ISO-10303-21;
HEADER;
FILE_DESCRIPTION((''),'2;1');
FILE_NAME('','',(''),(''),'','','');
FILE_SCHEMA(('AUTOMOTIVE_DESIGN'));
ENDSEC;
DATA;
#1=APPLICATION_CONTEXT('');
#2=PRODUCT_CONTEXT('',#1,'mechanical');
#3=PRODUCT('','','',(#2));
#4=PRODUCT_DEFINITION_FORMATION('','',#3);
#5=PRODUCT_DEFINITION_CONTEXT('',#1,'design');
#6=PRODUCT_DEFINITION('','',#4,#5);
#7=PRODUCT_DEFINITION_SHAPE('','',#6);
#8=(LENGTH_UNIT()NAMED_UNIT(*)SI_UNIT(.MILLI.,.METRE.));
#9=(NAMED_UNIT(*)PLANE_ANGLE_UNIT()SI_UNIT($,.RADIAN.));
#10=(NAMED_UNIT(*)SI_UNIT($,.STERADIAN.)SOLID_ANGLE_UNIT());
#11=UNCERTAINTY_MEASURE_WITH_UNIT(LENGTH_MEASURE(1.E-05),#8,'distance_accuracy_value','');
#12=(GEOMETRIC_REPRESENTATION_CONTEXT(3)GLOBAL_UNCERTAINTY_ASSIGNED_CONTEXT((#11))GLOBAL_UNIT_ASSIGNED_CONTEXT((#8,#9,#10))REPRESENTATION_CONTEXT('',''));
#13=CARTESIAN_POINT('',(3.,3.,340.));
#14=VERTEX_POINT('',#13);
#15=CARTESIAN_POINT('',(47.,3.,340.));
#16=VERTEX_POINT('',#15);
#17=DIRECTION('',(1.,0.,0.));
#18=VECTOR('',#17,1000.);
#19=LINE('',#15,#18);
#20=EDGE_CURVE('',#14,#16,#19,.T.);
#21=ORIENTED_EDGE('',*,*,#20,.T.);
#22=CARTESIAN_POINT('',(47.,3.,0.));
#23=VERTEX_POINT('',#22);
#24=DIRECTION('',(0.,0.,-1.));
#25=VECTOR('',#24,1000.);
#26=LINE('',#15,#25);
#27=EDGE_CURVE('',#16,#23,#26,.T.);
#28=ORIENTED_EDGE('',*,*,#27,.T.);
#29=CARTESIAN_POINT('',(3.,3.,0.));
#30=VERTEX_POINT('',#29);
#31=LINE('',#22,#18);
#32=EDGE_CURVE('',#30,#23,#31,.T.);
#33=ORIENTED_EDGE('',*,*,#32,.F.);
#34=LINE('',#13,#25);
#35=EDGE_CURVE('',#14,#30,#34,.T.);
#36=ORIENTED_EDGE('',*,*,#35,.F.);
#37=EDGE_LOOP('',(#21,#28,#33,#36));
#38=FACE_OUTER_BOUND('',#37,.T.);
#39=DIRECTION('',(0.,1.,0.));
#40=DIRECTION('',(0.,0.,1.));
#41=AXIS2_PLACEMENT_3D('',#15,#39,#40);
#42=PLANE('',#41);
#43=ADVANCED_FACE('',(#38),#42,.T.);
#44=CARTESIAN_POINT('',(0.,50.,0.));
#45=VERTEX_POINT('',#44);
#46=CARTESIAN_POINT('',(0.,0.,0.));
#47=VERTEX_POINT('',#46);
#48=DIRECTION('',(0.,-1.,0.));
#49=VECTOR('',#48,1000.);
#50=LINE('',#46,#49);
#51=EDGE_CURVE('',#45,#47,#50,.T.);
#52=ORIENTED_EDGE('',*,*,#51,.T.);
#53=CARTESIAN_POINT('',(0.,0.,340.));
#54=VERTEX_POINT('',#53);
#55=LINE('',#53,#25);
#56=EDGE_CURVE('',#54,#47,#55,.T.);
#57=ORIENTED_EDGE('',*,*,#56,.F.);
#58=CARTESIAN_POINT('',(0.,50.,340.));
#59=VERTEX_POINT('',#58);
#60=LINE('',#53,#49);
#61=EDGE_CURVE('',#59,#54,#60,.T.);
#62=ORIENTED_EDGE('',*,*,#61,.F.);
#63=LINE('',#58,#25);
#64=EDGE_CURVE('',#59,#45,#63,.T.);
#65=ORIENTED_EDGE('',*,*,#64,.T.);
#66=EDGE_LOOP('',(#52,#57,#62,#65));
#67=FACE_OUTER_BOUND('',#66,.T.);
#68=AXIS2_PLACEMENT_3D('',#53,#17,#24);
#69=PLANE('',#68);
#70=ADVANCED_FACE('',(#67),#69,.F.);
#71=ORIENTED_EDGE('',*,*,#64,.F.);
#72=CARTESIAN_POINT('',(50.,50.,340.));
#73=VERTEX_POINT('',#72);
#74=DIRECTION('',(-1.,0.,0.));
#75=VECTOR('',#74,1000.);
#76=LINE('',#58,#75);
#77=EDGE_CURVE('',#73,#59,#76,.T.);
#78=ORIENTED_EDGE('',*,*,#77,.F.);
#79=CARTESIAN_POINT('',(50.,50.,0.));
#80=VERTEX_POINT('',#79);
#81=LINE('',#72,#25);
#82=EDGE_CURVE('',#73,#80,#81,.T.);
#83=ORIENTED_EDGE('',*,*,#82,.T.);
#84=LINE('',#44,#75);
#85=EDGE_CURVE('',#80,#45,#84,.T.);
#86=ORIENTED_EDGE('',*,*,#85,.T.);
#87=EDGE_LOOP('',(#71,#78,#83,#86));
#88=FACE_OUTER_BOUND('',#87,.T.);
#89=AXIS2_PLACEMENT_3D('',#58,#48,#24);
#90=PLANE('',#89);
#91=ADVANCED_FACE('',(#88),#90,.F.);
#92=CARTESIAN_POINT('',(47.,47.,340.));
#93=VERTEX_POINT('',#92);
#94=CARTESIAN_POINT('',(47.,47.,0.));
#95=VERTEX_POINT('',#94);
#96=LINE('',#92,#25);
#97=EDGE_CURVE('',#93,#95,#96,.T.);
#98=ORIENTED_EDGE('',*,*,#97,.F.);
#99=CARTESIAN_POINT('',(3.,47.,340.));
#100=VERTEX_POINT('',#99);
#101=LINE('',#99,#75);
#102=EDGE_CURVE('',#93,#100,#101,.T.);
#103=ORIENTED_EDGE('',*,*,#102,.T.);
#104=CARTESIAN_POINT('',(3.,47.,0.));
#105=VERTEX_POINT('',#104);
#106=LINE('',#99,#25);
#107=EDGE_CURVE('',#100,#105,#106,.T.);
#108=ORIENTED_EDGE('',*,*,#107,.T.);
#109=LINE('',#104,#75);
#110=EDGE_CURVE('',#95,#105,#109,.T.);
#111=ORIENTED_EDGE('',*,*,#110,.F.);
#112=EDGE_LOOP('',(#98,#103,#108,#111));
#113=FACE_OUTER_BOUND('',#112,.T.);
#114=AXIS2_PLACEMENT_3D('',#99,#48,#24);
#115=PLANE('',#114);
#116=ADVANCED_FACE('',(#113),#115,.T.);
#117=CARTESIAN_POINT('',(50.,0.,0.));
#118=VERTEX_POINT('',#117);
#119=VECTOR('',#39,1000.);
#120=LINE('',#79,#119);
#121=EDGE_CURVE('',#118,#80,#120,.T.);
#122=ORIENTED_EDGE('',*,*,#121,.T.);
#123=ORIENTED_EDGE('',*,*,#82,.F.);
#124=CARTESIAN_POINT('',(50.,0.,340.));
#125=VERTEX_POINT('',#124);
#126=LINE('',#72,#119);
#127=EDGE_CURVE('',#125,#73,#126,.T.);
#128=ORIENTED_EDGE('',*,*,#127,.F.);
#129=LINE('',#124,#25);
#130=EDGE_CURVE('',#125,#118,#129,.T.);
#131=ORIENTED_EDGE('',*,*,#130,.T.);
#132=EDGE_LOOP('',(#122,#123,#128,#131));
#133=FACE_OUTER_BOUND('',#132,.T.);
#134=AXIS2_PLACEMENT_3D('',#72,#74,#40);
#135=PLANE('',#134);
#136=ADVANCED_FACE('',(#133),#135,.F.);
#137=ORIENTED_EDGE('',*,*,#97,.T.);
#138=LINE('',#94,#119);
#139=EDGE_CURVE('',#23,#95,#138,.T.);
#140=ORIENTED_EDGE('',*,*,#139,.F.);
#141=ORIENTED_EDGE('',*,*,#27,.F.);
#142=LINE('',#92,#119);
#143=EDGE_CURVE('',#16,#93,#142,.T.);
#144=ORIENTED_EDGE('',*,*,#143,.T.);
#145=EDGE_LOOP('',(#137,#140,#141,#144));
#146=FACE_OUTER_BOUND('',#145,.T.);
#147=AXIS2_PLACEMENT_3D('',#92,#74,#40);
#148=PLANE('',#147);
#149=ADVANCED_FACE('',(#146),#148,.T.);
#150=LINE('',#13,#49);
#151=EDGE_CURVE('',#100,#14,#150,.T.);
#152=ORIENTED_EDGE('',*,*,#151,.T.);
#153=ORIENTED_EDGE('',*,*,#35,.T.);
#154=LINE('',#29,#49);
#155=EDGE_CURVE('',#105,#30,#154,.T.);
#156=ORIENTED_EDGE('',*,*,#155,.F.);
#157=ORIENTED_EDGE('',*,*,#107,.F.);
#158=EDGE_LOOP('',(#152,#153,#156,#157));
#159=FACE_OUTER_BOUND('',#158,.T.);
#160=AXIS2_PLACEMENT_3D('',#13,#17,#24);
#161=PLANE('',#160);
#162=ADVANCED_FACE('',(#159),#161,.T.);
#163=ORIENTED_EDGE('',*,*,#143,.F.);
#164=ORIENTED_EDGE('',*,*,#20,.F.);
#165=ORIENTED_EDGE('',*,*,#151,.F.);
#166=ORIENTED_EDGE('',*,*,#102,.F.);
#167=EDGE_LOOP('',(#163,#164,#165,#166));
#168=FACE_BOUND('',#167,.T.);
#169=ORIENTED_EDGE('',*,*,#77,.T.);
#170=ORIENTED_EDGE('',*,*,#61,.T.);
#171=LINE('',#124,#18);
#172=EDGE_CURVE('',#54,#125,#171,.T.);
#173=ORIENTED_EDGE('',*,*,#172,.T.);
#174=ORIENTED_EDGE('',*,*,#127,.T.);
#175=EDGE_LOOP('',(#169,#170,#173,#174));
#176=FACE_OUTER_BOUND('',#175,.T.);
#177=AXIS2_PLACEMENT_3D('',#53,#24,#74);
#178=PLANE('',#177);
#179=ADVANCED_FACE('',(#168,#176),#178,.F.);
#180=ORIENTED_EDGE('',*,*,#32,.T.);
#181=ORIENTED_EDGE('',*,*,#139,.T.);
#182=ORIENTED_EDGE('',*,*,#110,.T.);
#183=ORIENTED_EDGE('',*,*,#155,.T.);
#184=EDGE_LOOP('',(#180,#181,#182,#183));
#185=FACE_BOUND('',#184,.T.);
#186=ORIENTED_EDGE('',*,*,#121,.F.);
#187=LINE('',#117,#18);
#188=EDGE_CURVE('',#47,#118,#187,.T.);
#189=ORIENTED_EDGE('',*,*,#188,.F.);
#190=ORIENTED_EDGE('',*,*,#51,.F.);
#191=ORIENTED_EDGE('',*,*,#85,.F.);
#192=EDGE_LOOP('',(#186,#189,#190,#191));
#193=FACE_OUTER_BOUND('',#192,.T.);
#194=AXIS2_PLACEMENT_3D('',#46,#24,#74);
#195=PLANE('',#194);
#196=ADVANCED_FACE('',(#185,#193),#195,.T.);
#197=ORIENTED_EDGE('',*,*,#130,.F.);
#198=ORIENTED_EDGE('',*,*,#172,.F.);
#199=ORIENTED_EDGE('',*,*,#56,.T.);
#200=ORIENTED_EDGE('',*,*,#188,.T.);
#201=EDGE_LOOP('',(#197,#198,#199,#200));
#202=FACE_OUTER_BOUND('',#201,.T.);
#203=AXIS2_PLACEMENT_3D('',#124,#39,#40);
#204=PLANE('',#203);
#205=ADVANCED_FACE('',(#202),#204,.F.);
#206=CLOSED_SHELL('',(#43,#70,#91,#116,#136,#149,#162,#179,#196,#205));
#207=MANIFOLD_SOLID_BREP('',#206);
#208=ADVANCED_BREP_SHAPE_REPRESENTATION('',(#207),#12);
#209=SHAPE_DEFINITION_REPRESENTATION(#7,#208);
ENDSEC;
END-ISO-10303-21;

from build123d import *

# Parameters (mm, degrees)
SKETCH_1_W      = 50
SKETCH_1_H      = 50
SKETCH_1_W_2    = 44
SKETCH_1_H_2    = 44
EXTRUDE_2_DEPTH = 340


with BuildPart() as part:
    # 草图1 → 凸台-拉伸2 (new body)
    with BuildSketch(Plane.XY):
        with Locations((25, 25)):
            Rectangle(SKETCH_1_W, SKETCH_1_H)
        with Locations((25, 25)):
            Rectangle(SKETCH_1_W_2, SKETCH_1_H_2, mode=Mode.SUBTRACT)
    extrude(amount=EXTRUDE_2_DEPTH)


solid = part.part
